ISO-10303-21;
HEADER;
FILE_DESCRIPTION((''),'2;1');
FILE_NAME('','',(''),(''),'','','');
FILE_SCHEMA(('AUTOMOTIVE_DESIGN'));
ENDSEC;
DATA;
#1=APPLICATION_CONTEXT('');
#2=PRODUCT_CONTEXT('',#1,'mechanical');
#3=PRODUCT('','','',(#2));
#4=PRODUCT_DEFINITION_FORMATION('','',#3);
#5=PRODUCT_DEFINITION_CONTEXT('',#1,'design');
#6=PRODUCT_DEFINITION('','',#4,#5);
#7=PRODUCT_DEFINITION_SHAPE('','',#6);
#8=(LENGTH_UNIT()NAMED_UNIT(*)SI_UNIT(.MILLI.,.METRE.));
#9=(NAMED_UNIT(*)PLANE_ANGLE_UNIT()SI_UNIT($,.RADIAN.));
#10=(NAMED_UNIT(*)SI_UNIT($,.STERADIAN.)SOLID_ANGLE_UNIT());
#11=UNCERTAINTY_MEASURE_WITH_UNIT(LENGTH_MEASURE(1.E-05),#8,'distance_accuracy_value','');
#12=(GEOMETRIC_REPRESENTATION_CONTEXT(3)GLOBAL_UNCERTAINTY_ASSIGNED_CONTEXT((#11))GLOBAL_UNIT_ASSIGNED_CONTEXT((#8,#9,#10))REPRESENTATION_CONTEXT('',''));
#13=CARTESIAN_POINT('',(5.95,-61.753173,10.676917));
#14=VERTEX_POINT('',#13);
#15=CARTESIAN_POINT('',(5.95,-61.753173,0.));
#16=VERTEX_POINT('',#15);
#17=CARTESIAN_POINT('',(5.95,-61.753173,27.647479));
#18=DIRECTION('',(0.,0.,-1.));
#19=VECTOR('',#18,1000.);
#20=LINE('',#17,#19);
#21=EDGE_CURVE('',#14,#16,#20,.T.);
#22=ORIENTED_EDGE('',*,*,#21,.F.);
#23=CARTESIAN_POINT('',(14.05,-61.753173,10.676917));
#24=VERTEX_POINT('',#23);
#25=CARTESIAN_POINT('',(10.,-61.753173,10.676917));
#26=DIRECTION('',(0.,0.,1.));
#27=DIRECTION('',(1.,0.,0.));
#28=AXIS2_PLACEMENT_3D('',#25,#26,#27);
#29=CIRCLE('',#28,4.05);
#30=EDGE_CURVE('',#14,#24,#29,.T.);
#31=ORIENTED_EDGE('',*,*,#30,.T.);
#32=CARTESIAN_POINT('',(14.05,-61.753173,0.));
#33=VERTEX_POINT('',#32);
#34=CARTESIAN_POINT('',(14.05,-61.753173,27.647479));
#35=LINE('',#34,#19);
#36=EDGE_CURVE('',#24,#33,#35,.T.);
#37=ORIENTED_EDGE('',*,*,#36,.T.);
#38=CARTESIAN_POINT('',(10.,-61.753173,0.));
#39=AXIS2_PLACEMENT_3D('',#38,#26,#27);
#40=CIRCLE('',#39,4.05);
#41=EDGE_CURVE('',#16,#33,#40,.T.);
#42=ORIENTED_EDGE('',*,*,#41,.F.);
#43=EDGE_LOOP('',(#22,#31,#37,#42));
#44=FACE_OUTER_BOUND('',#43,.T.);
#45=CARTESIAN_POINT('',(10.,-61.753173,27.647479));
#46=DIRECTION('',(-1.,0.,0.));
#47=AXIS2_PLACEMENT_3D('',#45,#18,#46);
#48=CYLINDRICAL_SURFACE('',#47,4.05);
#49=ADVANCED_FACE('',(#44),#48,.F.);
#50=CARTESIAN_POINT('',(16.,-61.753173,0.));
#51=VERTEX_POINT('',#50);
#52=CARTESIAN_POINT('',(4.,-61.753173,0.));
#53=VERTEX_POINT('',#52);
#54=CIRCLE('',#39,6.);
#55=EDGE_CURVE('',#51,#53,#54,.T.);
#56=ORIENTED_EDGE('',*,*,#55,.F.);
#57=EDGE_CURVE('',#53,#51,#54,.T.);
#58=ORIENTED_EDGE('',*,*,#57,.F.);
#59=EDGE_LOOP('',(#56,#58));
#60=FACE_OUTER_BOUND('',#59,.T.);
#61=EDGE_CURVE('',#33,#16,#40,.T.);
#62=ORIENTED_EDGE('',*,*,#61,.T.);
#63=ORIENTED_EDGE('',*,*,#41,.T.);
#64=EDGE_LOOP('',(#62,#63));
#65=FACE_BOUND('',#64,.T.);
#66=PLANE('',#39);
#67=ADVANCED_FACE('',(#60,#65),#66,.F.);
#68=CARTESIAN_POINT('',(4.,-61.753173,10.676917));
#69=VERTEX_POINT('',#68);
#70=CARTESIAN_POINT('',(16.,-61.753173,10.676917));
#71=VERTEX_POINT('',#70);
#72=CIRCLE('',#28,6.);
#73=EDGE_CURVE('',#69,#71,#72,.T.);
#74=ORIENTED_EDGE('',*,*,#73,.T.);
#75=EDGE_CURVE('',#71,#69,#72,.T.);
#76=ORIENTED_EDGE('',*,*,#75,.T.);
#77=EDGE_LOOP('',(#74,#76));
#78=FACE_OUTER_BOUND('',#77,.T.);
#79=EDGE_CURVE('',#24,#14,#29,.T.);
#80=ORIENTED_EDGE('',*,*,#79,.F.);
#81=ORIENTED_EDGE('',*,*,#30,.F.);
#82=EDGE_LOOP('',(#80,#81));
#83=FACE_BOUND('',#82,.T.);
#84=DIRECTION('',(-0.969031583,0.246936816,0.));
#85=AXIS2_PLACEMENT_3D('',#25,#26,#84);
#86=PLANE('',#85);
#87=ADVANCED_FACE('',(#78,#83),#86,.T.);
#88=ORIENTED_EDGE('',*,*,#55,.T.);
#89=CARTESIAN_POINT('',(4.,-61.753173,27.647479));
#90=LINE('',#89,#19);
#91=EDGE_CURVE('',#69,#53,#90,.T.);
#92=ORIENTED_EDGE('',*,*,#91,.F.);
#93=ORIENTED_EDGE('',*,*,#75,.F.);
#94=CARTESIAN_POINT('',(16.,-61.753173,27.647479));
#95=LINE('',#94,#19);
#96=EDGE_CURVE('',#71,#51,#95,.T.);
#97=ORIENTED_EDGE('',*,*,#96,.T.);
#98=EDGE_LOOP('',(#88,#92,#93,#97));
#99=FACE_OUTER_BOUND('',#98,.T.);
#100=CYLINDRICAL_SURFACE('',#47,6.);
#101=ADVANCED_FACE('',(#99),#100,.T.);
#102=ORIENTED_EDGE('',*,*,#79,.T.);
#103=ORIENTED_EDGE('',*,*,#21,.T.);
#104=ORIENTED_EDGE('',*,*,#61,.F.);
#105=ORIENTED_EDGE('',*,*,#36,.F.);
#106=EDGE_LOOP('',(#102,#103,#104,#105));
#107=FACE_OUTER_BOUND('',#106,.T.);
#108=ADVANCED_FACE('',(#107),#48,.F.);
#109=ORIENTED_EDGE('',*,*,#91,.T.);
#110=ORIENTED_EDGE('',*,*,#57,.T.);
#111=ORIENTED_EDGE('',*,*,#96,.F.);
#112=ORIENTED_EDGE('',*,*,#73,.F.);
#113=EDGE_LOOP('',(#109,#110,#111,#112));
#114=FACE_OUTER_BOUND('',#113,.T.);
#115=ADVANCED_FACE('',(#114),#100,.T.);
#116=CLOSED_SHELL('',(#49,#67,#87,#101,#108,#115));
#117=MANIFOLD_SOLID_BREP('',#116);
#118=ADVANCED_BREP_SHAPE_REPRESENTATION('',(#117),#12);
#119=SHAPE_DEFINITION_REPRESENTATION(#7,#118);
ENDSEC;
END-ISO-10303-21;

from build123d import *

# Parameters (mm, degrees)
SKETCH1_R           = 6
SKETCH1_R_2         = 4.05
BOSS_EXTRUDE1_DEPTH = 10.676916711


with BuildPart() as part:
    # Sketch1 → Boss-Extrude1 (new body)
    with BuildSketch(Plane.XY):
        with Locations(Location((10, -61.753173354, 0), (0, 0, 180))):
            Circle(SKETCH1_R)
        with Locations(Location((10, -61.753173354, 0), (0, 0, 180))):
            Circle(SKETCH1_R_2, mode=Mode.SUBTRACT)
    extrude(amount=BOSS_EXTRUDE1_DEPTH)


solid = part.part
